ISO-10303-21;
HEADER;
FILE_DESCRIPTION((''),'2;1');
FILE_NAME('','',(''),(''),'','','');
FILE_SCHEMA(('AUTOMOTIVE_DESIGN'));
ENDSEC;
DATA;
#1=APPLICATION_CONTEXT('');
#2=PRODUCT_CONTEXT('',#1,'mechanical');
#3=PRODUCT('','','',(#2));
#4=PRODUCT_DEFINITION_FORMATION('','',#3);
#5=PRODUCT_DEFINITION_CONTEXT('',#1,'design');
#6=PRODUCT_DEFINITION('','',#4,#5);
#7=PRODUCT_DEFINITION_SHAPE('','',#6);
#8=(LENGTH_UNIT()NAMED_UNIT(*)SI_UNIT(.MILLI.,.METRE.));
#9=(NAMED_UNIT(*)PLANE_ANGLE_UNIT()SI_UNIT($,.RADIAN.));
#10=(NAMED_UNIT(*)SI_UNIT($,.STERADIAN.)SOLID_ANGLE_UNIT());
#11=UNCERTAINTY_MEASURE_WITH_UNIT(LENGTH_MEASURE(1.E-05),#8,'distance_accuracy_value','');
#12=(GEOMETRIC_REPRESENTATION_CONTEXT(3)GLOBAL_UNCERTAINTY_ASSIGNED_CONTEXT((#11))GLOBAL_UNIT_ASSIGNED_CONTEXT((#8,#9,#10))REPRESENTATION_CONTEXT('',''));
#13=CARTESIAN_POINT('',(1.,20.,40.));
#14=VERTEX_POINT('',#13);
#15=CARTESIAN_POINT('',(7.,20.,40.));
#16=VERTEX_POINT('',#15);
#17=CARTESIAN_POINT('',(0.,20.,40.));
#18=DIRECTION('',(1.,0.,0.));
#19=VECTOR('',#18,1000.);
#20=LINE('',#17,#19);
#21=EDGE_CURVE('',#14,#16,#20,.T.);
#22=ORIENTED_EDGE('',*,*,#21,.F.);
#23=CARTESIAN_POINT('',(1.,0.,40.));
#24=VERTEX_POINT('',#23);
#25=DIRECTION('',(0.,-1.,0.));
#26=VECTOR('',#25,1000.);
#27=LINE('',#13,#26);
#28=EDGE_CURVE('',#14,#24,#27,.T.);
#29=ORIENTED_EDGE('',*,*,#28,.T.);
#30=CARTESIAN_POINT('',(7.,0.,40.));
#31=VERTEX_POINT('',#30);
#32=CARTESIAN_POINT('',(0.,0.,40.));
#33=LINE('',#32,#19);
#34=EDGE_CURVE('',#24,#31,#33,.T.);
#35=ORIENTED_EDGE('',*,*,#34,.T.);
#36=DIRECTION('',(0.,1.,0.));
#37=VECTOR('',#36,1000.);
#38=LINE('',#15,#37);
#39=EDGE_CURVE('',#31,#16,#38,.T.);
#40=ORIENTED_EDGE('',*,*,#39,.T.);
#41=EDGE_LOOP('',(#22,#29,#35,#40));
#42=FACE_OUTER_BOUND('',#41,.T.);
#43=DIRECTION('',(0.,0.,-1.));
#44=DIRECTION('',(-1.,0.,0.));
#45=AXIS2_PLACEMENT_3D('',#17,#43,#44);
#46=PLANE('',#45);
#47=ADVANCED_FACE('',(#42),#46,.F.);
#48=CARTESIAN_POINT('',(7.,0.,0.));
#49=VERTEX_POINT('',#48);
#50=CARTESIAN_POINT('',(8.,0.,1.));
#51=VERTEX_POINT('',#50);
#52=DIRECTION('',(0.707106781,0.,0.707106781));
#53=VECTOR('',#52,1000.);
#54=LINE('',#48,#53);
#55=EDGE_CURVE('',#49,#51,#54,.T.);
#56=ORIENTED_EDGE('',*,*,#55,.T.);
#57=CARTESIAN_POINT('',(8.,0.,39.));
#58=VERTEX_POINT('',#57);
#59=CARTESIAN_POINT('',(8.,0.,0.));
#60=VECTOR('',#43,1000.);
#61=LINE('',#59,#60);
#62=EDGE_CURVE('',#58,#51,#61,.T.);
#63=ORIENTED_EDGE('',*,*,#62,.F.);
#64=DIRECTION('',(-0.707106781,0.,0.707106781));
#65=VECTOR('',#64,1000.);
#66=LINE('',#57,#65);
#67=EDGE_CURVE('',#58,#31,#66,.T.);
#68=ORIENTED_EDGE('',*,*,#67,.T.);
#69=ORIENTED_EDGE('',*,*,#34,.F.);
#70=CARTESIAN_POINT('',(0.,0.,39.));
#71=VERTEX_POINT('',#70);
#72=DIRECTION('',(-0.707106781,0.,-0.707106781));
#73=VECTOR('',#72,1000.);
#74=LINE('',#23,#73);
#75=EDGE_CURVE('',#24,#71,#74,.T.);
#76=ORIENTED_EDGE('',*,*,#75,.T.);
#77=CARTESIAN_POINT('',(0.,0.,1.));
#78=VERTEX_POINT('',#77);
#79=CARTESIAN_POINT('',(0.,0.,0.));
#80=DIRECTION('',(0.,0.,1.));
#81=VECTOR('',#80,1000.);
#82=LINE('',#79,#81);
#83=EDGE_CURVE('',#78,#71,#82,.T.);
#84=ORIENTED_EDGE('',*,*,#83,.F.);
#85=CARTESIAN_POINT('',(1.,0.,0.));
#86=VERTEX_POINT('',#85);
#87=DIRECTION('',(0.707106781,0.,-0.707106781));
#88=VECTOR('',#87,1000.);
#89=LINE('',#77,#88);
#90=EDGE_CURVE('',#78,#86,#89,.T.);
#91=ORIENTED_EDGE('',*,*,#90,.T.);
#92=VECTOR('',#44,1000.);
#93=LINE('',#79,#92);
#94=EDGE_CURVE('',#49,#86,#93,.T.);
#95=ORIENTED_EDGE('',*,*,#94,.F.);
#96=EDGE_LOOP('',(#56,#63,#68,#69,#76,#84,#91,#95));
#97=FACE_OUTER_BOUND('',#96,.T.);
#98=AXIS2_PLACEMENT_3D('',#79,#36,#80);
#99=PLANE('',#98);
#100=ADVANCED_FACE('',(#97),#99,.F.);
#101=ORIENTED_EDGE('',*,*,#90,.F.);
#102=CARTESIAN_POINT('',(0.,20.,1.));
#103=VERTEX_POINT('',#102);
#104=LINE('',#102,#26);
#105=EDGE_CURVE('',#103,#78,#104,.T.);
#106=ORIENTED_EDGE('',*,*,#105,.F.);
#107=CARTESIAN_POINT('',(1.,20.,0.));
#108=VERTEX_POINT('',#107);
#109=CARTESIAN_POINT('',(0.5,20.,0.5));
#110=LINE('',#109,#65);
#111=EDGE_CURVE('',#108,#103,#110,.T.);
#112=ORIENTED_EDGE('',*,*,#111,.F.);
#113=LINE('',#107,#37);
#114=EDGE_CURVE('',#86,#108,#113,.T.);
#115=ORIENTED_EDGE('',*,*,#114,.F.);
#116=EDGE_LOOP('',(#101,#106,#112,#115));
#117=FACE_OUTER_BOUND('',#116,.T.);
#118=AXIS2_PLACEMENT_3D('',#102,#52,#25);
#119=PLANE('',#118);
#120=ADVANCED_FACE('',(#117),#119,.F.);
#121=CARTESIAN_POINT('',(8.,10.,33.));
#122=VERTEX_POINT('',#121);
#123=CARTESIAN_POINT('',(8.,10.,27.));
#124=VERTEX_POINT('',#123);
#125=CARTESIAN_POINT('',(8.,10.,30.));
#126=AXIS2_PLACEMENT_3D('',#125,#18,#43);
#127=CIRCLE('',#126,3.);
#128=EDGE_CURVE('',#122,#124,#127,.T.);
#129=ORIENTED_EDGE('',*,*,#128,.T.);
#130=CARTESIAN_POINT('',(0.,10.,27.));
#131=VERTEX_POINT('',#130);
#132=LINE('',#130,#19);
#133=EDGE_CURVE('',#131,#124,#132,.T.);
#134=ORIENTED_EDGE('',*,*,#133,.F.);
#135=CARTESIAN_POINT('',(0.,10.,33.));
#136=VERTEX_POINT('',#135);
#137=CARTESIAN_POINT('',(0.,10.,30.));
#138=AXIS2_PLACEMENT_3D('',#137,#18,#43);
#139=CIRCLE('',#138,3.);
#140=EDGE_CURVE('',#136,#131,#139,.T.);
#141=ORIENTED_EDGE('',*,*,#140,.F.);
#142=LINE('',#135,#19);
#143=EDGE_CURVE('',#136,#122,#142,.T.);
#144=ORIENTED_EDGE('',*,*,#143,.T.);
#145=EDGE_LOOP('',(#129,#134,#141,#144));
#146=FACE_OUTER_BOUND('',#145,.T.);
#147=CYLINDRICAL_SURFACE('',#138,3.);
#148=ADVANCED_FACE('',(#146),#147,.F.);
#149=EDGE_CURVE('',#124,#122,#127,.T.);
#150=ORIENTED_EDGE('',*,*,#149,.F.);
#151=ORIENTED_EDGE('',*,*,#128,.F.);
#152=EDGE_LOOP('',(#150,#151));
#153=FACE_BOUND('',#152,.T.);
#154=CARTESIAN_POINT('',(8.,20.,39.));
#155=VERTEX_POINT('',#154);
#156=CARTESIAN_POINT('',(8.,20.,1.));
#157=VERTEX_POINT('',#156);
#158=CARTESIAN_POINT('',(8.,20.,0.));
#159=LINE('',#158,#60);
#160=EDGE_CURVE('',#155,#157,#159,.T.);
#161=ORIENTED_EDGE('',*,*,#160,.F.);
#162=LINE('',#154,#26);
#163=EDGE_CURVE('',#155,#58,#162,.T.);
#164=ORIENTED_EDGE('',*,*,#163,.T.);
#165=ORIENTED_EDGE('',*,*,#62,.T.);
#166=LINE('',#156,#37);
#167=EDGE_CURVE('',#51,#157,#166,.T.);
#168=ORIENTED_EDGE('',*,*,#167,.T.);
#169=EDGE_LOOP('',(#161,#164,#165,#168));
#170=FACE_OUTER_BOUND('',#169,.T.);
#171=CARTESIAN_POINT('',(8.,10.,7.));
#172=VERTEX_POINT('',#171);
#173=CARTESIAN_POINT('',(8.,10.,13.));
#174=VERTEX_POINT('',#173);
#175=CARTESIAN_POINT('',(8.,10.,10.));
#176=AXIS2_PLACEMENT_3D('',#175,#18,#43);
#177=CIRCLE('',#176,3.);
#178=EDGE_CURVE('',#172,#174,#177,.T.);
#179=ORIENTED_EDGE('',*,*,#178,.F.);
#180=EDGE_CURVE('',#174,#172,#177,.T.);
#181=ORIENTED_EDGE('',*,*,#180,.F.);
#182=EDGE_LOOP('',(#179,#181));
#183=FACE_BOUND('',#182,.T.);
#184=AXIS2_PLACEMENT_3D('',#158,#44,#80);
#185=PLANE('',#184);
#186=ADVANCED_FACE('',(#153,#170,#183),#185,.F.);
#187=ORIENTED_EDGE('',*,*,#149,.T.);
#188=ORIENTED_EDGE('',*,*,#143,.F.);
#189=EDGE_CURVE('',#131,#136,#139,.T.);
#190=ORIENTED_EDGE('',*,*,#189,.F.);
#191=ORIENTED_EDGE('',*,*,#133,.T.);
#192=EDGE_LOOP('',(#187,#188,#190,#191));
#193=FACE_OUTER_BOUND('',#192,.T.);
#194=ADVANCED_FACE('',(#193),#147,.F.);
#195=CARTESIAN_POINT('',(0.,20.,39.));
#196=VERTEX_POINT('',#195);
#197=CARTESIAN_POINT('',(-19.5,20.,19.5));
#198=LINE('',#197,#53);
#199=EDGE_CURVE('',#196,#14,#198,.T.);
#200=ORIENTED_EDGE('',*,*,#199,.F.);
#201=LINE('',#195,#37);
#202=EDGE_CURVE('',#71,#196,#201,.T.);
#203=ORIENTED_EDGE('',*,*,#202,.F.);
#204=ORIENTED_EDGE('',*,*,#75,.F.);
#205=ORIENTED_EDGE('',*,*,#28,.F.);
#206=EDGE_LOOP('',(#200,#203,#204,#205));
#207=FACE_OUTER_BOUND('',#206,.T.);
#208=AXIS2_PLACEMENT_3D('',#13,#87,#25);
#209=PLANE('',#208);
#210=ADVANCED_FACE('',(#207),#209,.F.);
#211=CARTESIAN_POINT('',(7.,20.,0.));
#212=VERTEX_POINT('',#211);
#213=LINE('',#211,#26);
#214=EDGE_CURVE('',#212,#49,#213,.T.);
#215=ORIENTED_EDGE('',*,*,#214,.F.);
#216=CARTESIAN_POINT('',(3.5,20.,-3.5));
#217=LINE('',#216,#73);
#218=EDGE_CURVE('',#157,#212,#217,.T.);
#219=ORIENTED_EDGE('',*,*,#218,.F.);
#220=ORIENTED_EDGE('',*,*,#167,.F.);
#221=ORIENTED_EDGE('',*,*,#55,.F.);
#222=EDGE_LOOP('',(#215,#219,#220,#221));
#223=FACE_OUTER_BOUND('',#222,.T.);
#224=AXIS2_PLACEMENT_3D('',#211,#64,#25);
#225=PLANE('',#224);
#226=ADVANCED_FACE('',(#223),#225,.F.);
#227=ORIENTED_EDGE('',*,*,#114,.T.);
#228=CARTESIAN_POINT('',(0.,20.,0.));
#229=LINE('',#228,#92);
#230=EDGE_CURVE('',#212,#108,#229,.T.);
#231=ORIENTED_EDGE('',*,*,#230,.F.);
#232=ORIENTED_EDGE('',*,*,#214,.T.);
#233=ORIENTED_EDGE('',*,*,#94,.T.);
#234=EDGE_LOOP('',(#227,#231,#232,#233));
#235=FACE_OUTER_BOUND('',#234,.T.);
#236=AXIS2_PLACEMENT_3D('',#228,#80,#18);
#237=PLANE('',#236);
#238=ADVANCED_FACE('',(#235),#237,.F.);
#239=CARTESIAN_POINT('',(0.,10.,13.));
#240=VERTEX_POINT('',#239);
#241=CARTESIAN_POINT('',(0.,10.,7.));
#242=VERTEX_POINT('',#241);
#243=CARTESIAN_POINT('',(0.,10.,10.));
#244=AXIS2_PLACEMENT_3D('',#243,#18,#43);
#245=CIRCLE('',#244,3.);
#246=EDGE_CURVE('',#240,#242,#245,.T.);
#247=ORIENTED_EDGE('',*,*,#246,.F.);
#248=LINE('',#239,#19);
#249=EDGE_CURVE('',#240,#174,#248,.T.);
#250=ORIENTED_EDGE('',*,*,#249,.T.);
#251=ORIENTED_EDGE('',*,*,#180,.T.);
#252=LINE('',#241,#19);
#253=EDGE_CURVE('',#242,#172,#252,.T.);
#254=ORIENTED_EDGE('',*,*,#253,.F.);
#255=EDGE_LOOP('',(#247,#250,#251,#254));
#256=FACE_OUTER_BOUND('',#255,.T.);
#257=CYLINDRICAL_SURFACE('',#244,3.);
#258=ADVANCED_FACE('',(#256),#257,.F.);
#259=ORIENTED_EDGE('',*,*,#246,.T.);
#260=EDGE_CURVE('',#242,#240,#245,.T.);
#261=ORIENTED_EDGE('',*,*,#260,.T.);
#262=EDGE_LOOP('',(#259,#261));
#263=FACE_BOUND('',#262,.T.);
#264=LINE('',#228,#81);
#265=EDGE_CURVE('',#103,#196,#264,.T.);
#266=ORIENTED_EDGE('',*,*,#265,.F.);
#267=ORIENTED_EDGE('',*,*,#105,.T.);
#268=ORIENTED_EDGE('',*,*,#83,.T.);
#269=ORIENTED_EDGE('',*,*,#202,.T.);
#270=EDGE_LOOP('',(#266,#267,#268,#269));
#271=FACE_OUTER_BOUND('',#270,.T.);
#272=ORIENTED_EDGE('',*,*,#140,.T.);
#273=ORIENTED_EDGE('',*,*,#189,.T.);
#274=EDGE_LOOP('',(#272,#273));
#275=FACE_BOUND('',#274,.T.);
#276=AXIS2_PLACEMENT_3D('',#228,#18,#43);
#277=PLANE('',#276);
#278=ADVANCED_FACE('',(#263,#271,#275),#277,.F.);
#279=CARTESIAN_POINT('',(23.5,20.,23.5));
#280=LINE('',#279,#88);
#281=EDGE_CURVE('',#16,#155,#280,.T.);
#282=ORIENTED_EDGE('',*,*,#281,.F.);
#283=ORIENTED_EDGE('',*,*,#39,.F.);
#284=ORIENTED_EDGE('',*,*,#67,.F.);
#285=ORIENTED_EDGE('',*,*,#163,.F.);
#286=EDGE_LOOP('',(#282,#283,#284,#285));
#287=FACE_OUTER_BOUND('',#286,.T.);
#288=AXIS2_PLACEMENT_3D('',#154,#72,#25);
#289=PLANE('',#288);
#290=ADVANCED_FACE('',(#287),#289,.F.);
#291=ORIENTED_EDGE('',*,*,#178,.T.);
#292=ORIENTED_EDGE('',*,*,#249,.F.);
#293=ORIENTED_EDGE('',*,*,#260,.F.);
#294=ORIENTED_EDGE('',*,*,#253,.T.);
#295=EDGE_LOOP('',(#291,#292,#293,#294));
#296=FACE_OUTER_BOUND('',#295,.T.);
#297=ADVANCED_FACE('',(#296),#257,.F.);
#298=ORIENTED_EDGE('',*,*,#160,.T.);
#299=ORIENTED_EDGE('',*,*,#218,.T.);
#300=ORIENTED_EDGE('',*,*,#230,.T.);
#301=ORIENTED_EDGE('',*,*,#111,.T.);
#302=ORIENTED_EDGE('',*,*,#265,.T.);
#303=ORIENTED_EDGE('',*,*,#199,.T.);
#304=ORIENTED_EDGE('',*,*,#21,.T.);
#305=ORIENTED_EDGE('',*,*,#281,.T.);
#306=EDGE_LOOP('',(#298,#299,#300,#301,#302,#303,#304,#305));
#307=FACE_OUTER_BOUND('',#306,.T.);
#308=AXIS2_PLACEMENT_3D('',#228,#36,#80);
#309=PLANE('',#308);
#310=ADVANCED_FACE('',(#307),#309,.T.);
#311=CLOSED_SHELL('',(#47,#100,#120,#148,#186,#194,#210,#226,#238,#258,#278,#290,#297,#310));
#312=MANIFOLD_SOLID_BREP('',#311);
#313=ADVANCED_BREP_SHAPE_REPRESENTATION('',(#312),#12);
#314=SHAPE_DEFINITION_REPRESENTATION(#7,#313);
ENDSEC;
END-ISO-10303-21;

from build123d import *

# Parameters (mm, degrees)
SKETCH1_W           = 8
SKETCH1_H           = 40
BOSS_EXTRUDE1_DEPTH = 20
CHAMFER1_SIZE       = 1
SKETCH2_R           = 3
CUT_EXTRUDE1_DEPTH  = 46.431266766


with BuildPart() as part:
    # Sketch1 → Boss-Extrude1 (new body)
    with BuildSketch(Plane(origin=(0, 0, 0), x_dir=(1, 0, 0), z_dir=(0, 1, 0))):
        with Locations((4, -20)):
            Rectangle(SKETCH1_W, SKETCH1_H)
    extrude(amount=BOSS_EXTRUDE1_DEPTH)

    # Chamfer1
    chamfer1_edges = [part.edges().sort_by_distance(p)[0] for p in [
        (0, 10, 0),
        (8, 10, 0),
        (8, 10, 40),
        (0, 10, 40),
    ]]
    chamfer(chamfer1_edges, length=CHAMFER1_SIZE)

    # Sketch2 → Cut-Extrude1 (cut, through all)
    with BuildSketch(Plane(origin=(8, 0, 0), x_dir=(0, 0, -1), z_dir=(1, 0, 0))):
        with Locations((-30, 10)):
            Circle(SKETCH2_R)
        with Locations((-10, 10)):
            Circle(SKETCH2_R)
    extrude(amount=-CUT_EXTRUDE1_DEPTH, mode=Mode.SUBTRACT)


solid = part.part
